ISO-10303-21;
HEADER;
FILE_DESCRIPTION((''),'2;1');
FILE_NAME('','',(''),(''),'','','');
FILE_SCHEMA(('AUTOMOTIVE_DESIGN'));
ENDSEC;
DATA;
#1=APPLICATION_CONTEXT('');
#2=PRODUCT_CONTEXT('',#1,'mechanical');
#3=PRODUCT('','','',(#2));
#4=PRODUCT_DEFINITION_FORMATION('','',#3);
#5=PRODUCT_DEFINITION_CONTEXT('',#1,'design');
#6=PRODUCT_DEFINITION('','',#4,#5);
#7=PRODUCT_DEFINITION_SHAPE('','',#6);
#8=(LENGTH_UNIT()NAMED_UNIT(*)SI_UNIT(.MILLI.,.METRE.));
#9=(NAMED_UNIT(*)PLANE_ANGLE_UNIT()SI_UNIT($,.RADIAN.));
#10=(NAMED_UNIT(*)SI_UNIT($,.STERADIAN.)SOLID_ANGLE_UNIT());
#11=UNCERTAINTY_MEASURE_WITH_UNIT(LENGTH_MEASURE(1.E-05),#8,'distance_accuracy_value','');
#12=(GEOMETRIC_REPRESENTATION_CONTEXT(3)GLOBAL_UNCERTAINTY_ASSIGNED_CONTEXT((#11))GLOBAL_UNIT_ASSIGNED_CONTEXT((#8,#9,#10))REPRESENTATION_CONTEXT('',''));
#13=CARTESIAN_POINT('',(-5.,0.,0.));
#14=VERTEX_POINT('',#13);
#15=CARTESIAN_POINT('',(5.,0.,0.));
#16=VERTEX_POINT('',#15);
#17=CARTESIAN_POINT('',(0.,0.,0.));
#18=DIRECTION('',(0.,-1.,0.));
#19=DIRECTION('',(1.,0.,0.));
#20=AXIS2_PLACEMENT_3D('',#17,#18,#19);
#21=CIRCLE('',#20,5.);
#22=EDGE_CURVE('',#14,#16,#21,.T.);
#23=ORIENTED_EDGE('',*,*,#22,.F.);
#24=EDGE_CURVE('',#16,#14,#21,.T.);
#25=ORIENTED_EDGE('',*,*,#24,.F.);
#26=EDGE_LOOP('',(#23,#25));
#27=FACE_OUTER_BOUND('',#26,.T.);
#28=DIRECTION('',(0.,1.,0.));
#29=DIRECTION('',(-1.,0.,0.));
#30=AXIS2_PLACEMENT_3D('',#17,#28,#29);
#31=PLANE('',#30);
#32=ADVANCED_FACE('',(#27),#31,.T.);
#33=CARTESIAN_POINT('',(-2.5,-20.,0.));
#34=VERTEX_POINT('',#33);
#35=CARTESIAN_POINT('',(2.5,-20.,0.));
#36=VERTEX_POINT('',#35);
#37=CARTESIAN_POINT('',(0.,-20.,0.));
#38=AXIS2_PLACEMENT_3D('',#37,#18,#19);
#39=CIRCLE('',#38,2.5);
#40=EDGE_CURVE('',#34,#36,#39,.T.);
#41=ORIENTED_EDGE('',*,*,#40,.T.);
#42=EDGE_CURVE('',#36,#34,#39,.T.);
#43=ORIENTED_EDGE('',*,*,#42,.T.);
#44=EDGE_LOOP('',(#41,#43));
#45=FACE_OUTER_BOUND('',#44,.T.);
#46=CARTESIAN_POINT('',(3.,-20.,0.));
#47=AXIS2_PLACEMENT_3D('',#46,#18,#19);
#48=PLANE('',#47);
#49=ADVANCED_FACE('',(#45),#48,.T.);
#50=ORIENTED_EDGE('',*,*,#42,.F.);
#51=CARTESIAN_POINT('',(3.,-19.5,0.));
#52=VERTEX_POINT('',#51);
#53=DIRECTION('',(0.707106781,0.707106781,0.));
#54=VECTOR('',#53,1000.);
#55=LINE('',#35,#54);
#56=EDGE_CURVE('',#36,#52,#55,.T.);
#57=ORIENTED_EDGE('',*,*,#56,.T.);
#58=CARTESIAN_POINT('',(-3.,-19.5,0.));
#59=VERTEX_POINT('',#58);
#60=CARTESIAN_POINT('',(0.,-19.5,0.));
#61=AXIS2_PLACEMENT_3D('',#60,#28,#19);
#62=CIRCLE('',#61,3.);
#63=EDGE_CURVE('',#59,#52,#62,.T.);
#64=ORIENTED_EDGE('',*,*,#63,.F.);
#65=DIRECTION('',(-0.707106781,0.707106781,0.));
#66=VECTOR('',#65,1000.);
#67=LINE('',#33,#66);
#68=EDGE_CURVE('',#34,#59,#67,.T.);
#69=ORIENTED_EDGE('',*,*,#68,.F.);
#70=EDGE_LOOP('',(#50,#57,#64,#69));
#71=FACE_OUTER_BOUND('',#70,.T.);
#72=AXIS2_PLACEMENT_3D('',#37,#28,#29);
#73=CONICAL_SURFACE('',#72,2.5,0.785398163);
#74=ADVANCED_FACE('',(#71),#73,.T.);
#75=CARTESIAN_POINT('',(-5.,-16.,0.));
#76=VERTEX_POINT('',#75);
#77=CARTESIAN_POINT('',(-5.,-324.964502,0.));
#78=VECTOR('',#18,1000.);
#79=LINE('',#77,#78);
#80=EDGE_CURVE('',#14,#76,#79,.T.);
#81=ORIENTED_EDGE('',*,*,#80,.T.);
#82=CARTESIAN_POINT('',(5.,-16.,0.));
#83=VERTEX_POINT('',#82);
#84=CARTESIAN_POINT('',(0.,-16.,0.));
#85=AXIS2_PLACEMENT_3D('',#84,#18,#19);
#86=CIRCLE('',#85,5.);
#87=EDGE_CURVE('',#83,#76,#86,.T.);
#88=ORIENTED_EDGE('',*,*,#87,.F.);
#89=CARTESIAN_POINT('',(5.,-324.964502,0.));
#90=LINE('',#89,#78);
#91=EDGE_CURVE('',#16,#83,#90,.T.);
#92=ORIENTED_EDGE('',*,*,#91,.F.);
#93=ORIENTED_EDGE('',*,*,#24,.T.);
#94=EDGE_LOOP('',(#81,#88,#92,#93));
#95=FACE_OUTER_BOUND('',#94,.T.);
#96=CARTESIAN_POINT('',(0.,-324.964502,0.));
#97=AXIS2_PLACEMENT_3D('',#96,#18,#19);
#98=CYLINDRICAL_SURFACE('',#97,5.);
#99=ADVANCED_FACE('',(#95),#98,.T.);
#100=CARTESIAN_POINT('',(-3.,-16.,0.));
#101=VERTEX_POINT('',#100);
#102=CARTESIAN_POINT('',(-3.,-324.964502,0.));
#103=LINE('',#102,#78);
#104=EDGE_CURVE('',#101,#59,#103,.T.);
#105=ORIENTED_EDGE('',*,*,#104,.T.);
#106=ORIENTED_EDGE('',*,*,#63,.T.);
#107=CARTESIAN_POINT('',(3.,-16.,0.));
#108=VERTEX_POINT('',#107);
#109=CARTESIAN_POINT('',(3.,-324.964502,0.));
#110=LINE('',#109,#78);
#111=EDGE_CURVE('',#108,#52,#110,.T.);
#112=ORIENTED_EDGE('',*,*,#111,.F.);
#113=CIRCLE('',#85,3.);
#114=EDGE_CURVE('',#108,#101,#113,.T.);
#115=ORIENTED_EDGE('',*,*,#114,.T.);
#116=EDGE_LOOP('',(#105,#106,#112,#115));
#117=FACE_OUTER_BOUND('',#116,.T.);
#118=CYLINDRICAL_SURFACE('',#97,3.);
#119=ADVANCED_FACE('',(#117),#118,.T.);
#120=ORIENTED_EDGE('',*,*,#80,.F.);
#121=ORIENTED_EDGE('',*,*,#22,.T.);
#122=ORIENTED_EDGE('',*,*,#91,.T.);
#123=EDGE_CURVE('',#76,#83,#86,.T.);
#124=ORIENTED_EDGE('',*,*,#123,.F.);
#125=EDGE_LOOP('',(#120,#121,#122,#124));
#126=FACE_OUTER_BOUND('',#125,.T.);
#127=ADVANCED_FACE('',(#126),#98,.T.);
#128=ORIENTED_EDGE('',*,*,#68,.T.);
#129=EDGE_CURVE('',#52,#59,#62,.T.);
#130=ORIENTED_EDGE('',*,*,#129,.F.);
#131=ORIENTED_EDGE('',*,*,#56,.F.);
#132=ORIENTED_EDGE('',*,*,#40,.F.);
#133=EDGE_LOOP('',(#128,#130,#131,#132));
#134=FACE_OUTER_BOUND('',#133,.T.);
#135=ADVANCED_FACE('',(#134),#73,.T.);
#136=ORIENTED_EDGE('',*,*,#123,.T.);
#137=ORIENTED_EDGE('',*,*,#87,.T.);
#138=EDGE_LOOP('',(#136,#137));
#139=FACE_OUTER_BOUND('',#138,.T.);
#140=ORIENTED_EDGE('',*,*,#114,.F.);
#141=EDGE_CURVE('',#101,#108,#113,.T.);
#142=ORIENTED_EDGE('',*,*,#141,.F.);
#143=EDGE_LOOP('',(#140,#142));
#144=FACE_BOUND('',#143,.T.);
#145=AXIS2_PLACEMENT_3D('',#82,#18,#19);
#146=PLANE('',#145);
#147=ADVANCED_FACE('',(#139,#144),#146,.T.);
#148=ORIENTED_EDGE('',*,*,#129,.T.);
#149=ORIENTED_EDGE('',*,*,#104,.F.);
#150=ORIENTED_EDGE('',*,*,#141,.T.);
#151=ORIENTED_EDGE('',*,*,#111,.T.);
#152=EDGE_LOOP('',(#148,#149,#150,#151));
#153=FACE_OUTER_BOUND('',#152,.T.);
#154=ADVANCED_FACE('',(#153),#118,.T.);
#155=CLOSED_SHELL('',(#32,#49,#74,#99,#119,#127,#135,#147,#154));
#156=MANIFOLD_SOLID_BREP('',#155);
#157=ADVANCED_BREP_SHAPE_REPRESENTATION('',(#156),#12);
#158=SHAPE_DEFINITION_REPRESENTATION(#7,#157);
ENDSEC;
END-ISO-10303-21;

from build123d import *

# Parameters (mm, degrees)
CHAMFER2_SIZE = 0.5


with BuildPart() as part:
    # Sketch1 → Revolve1 (revolve)
    with BuildSketch(Plane.XY):
        Polygon((0, 0), (5, 0), (5, -16), (3, -16), (3, -20), (0, -20), align=None)
    revolve(axis=Axis((0, -324.964502388, 0), (0, 1, 0)))

    # Chamfer2
    chamfer2_edges = [part.edges().sort_by_distance(p)[0] for p in [
        (-3, -20, 0),
    ]]
    chamfer(chamfer2_edges, length=CHAMFER2_SIZE)


solid = part.part
